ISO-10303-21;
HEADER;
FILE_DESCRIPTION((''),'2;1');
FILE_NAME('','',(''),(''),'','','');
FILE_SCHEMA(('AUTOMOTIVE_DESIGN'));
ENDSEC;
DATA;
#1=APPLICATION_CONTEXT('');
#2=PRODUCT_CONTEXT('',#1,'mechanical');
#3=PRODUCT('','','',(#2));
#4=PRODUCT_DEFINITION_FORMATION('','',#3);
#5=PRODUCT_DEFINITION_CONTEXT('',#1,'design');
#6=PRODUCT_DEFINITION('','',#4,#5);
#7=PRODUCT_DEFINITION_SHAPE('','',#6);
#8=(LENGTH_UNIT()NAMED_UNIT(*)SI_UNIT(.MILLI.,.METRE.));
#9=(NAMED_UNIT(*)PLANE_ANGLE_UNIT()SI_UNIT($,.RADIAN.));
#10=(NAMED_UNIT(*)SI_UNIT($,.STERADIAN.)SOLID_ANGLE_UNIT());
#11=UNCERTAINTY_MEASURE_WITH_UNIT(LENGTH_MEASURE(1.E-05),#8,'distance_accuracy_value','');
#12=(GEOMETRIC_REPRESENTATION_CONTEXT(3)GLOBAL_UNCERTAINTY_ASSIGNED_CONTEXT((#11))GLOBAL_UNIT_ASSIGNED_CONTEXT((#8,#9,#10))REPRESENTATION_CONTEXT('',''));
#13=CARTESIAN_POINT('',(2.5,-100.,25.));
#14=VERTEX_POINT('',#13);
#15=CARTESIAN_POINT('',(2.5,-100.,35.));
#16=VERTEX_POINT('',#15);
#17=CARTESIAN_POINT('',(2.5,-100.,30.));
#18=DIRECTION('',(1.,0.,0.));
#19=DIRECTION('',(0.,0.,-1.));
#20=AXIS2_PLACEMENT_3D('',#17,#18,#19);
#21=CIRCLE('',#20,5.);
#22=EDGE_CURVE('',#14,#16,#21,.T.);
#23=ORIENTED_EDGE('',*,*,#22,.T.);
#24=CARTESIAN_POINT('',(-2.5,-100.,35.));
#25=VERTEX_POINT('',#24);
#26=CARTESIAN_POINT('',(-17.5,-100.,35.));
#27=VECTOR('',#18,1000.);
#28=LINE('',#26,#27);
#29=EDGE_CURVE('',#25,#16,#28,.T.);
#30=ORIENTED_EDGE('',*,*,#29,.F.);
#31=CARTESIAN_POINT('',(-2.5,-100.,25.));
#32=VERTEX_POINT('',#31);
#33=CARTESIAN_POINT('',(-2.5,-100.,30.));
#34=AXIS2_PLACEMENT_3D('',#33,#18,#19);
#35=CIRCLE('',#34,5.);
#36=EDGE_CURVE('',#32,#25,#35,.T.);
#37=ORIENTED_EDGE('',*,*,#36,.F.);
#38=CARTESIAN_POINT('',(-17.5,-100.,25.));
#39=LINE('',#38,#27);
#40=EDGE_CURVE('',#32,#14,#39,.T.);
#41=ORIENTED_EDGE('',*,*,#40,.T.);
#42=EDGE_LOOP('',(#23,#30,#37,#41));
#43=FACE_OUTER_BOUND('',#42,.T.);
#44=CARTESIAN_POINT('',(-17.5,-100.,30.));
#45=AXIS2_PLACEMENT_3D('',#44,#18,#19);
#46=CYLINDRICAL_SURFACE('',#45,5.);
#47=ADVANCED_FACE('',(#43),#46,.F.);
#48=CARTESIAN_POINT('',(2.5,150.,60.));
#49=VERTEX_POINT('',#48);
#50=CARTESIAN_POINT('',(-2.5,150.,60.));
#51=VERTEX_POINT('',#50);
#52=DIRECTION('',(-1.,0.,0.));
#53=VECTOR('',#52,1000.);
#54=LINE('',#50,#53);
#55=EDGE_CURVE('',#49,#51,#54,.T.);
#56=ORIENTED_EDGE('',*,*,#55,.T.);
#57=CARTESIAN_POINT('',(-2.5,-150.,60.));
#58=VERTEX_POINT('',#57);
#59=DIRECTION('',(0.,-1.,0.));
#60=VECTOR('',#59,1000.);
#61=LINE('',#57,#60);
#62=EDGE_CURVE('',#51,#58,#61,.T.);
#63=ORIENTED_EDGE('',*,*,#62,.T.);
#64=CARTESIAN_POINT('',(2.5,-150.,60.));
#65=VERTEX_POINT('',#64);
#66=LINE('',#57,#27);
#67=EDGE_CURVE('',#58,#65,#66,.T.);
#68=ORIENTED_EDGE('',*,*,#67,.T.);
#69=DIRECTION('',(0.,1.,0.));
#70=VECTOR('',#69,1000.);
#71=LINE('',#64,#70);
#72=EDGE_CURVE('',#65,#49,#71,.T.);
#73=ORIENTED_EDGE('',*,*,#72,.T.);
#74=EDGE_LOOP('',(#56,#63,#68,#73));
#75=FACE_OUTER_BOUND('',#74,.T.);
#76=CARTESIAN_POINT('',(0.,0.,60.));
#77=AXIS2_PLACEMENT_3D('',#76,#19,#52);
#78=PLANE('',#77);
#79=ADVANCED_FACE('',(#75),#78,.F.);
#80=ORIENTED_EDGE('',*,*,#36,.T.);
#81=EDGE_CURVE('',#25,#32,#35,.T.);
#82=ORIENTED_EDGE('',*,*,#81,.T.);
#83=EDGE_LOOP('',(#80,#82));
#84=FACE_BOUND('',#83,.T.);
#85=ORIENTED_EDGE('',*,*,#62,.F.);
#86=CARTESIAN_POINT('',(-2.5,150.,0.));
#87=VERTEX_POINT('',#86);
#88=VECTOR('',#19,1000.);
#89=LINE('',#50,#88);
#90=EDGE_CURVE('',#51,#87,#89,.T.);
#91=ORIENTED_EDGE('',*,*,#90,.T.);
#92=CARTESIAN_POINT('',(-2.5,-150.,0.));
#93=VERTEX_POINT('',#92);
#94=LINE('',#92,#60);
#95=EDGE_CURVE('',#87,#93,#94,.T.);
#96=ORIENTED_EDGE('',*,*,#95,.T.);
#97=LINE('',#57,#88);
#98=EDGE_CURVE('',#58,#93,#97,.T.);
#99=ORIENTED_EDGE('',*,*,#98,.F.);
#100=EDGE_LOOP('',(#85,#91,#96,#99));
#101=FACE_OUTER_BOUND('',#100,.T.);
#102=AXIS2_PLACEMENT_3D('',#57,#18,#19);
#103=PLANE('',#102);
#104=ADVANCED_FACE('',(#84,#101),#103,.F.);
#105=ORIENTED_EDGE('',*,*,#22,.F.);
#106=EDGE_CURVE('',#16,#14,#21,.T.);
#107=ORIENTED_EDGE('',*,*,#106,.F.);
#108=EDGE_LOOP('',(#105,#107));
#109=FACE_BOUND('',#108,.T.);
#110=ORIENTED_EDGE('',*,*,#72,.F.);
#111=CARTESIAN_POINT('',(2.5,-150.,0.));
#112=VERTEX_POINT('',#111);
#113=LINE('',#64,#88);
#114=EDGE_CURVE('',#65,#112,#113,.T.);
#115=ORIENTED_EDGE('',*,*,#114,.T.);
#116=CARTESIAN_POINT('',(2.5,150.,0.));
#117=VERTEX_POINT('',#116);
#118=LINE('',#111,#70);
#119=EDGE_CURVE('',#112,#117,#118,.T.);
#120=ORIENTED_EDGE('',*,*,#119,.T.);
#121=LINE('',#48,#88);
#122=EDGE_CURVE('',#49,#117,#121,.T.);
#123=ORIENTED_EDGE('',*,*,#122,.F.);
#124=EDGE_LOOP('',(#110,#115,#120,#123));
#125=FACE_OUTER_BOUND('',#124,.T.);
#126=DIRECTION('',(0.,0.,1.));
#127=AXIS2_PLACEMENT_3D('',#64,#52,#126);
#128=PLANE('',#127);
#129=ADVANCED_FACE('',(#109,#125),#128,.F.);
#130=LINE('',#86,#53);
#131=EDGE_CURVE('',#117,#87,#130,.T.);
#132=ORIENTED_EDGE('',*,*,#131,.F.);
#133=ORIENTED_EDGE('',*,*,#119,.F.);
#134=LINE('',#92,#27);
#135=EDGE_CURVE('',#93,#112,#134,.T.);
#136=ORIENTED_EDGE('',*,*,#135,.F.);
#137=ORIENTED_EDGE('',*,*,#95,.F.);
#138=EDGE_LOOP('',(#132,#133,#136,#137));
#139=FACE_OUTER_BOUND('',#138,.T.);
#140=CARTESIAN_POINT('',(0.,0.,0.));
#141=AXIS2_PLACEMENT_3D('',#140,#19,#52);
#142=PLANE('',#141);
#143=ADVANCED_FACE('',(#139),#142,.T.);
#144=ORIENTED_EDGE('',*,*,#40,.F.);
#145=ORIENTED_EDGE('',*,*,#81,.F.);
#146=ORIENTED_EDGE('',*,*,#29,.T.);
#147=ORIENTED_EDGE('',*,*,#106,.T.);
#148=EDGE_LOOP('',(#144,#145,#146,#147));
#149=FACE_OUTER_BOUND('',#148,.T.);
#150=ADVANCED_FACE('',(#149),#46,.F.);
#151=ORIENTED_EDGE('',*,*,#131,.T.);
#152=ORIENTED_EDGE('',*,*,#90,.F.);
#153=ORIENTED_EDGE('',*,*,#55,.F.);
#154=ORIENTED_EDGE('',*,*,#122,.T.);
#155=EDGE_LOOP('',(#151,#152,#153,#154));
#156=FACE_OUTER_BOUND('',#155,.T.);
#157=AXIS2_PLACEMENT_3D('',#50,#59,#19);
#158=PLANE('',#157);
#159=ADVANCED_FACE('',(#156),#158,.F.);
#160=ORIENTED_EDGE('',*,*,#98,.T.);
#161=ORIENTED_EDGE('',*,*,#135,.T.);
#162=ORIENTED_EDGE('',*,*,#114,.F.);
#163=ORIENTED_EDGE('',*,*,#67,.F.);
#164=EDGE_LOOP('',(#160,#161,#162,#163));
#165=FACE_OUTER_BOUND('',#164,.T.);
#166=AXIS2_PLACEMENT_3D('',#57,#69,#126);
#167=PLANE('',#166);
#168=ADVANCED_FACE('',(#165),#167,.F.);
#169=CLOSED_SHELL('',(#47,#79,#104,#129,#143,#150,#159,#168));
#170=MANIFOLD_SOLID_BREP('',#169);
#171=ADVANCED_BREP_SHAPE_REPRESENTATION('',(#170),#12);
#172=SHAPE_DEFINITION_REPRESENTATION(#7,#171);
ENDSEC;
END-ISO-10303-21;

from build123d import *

# Parameters (mm, degrees)
SKETCH_1_W          = 5
SKETCH_1_H          = 300
EXTRUDE_1_DEPTH     = 60
SKETCH_2_R          = 5
CUT_EXTRUDE_1_DEPTH = 20


with BuildPart() as part:
    # 草图1 → 凸台-拉伸1 (new body)
    with BuildSketch(Plane.XY):
        Rectangle(SKETCH_1_W, SKETCH_1_H)
    extrude(amount=EXTRUDE_1_DEPTH)

    # 草图2 → 切除-拉伸1 (cut)
    with BuildSketch(Plane(origin=(2.5, 0, 0), x_dir=(0, 0, -1), z_dir=(1, 0, 0))):
        with Locations((-30, -100)):
            Circle(SKETCH_2_R)
    extrude(amount=-CUT_EXTRUDE_1_DEPTH, mode=Mode.SUBTRACT)


solid = part.part
